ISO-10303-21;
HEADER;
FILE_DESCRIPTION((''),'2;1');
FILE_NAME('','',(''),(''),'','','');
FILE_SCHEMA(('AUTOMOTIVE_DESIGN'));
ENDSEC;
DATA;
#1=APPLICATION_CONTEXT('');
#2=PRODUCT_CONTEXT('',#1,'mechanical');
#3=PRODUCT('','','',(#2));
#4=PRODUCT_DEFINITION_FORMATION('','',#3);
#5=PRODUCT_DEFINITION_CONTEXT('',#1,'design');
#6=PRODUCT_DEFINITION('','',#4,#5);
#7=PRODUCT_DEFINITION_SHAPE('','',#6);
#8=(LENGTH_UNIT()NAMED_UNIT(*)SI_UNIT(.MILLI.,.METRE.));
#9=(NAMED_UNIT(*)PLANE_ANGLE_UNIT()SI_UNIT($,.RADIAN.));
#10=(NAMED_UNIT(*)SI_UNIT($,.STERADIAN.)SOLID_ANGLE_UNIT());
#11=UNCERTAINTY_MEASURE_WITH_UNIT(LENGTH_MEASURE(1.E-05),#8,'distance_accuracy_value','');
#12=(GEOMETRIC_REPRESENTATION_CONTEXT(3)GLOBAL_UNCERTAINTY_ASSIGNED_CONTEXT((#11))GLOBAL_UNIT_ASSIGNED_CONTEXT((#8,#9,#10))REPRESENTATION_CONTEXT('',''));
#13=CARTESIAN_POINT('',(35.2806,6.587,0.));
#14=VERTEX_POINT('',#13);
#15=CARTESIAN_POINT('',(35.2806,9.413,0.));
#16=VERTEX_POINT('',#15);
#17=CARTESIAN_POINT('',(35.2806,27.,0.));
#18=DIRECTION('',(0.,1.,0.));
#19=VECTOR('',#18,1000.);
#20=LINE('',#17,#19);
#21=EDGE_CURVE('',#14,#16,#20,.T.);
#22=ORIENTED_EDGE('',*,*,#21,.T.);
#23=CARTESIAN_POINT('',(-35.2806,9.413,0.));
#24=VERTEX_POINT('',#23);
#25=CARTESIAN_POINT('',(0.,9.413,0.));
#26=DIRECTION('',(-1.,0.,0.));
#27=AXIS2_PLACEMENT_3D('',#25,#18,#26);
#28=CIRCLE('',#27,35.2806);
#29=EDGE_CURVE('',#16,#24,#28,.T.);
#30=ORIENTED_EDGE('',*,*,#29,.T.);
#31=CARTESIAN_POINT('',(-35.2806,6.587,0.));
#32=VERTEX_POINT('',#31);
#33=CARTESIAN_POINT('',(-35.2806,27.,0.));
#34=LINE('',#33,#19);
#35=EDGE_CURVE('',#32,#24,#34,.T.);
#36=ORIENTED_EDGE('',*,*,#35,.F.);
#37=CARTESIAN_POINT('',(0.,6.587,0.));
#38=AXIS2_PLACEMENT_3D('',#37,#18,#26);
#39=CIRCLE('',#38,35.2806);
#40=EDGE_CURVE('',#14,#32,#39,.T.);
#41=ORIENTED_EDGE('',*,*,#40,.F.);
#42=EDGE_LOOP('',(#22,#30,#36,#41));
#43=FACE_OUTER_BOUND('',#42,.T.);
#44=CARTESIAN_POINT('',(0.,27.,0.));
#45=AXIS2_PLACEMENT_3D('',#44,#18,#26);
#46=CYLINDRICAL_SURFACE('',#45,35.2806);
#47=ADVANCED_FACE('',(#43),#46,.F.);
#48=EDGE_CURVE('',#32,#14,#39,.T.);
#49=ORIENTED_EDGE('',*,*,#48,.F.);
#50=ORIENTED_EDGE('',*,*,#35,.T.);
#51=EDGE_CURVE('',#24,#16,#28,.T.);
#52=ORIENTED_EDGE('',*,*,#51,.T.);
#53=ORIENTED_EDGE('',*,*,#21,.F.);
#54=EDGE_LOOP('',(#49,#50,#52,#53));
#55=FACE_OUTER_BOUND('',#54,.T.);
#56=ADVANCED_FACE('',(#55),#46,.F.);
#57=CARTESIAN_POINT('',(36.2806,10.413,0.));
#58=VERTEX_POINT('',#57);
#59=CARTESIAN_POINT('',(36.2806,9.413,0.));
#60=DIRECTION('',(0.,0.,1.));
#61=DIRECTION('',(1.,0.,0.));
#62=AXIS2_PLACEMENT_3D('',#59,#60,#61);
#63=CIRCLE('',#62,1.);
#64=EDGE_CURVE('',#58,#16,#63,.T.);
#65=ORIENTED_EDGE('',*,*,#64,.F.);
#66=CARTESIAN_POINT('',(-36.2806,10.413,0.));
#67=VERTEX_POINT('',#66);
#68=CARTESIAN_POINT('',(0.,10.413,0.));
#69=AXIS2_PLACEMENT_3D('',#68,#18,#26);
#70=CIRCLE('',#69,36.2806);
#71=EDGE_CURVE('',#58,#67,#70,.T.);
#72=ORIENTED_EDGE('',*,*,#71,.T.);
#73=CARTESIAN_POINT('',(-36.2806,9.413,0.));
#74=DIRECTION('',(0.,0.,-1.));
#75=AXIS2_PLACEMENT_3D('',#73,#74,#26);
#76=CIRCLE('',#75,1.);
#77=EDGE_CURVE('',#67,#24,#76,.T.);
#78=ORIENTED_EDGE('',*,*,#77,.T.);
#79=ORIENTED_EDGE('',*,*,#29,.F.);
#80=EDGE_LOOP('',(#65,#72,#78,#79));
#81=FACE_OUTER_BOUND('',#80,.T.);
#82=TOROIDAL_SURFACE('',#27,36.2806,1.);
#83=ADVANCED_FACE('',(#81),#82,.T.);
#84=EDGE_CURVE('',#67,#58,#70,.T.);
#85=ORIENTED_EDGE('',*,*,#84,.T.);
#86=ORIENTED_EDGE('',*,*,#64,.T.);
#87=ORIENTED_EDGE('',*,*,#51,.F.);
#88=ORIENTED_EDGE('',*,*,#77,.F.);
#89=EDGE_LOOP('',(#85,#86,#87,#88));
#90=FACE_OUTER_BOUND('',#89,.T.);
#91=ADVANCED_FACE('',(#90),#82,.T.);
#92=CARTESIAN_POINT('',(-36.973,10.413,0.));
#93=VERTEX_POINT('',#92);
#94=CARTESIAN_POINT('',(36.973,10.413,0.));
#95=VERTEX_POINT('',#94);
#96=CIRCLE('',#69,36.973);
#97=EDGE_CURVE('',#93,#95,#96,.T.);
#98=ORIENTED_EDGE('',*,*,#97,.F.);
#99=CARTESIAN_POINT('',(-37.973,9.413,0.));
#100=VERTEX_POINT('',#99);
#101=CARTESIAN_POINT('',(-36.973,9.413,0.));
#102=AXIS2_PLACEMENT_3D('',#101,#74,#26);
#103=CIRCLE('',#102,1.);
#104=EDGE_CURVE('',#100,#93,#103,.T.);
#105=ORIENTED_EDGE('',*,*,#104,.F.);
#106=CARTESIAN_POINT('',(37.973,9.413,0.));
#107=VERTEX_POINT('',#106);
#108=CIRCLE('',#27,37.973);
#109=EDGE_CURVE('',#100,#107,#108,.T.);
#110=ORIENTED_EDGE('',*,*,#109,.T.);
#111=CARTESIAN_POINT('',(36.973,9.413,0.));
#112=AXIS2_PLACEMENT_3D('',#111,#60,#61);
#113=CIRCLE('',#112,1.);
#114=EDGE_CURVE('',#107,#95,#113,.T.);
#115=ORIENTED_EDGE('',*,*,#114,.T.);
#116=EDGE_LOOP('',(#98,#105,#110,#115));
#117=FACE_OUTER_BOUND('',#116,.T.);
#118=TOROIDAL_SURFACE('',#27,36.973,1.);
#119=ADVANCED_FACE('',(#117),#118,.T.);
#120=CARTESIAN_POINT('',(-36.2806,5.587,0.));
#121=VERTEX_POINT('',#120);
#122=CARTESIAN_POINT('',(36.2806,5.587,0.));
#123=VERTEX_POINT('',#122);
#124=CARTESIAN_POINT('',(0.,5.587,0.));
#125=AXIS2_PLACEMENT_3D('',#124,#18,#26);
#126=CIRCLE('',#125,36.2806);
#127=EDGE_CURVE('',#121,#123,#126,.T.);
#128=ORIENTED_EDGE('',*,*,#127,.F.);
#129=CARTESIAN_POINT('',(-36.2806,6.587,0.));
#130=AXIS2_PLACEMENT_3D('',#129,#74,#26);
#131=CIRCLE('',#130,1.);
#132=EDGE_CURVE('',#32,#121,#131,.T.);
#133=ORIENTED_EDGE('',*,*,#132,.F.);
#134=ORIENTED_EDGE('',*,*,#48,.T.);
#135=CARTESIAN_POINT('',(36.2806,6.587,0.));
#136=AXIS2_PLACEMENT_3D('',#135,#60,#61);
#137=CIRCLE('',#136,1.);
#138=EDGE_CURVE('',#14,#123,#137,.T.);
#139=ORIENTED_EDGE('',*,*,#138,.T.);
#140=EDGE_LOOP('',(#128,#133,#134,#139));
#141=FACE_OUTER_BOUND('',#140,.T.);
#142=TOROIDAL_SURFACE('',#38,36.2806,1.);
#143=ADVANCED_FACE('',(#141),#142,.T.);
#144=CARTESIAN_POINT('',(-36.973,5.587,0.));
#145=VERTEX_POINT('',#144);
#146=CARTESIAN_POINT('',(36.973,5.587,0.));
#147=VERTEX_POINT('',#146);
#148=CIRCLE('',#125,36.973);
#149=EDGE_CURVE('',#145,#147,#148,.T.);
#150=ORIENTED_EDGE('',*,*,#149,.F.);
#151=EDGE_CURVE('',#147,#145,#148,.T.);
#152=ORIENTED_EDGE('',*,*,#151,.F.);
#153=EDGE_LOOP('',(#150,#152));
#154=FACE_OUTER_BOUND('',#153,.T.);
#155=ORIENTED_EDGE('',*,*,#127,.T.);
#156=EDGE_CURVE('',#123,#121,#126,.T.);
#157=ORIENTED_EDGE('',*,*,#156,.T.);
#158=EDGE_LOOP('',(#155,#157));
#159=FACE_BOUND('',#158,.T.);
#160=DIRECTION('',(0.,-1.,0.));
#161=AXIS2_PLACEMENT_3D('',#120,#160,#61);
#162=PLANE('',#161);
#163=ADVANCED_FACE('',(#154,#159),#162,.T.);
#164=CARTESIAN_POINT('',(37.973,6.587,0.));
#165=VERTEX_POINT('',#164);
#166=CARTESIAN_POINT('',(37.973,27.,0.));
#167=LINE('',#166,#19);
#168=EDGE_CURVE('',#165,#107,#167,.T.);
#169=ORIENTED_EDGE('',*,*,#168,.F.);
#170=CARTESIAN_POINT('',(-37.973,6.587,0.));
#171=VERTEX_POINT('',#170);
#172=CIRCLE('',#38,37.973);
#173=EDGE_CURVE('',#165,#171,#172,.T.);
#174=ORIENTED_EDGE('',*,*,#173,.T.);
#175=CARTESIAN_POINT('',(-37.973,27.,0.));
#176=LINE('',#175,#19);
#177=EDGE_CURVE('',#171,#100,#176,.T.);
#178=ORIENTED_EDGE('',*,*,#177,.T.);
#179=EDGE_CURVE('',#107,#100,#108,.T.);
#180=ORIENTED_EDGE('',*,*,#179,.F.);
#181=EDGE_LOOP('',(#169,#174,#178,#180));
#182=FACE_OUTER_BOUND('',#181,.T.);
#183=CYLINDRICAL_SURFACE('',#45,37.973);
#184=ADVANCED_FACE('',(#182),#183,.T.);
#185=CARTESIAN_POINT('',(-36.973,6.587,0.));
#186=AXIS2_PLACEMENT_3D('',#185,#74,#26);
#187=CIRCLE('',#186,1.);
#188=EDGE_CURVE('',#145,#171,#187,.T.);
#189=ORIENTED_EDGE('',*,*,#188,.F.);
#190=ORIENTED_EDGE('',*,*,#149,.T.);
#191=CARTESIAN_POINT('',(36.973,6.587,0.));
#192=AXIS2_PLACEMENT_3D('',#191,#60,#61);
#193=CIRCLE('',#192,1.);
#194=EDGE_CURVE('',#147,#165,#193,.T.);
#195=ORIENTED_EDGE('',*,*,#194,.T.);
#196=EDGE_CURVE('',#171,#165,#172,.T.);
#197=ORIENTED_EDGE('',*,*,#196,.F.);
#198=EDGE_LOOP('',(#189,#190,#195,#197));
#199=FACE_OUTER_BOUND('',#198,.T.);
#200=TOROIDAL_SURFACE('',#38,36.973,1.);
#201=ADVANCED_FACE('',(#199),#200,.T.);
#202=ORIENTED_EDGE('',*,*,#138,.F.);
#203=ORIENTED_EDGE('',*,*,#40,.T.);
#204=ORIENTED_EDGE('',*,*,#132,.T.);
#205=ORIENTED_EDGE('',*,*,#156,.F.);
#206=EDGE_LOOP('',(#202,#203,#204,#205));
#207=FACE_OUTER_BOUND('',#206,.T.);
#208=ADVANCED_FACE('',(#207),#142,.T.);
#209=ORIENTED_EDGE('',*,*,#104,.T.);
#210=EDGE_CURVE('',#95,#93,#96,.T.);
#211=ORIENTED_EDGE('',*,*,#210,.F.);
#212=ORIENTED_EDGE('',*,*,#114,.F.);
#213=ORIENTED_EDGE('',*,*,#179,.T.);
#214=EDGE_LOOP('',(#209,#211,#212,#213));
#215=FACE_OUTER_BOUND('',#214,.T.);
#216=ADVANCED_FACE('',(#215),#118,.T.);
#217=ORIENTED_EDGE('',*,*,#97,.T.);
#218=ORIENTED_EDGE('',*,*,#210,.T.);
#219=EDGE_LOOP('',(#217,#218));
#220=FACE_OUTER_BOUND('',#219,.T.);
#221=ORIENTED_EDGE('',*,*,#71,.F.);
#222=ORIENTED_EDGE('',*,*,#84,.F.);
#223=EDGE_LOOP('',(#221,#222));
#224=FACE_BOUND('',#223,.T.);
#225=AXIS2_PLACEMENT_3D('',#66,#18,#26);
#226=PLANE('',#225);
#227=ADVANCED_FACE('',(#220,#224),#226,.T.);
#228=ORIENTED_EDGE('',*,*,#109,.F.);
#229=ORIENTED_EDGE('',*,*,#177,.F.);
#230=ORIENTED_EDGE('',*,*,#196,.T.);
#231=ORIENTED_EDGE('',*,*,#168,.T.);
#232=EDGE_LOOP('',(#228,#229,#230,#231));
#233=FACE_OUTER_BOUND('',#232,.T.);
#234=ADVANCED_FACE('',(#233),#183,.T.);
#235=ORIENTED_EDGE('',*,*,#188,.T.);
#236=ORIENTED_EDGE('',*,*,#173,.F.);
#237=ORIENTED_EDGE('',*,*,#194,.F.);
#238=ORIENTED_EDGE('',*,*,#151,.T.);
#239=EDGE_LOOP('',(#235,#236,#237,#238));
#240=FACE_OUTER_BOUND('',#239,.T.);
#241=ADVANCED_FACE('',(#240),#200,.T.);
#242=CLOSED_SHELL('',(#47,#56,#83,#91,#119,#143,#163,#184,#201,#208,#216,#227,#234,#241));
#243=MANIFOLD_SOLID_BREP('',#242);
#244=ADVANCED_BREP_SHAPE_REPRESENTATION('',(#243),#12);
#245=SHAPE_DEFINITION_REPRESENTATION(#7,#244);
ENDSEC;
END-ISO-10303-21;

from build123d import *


with BuildPart() as part:
    # 草图1 → 旋转1 (revolve)
    with BuildSketch(Plane.XY):
        with BuildLine():
            Line((-36.2806, 5.587), (-36.973, 5.587))
            ThreePointArc((-36.973, 5.587), (-37.680106781, 5.879893219), (-37.973, 6.587))
            Line((-37.973, 6.587), (-37.973, 9.413))
            ThreePointArc((-37.973, 9.413), (-37.680106781, 10.120106781), (-36.973, 10.413))
            Line((-36.973, 10.413), (-36.2806, 10.413))
            ThreePointArc((-36.2806, 10.413), (-35.573493219, 10.120106781), (-35.2806, 9.413))
            Line((-35.2806, 9.413), (-35.2806, 6.587))
            ThreePointArc((-35.2806, 6.587), (-35.573493219, 5.879893219), (-36.2806, 5.587))
        make_face()
    revolve(axis=Axis((0, 27, 0), (0, -1, 0)))


solid = part.part
